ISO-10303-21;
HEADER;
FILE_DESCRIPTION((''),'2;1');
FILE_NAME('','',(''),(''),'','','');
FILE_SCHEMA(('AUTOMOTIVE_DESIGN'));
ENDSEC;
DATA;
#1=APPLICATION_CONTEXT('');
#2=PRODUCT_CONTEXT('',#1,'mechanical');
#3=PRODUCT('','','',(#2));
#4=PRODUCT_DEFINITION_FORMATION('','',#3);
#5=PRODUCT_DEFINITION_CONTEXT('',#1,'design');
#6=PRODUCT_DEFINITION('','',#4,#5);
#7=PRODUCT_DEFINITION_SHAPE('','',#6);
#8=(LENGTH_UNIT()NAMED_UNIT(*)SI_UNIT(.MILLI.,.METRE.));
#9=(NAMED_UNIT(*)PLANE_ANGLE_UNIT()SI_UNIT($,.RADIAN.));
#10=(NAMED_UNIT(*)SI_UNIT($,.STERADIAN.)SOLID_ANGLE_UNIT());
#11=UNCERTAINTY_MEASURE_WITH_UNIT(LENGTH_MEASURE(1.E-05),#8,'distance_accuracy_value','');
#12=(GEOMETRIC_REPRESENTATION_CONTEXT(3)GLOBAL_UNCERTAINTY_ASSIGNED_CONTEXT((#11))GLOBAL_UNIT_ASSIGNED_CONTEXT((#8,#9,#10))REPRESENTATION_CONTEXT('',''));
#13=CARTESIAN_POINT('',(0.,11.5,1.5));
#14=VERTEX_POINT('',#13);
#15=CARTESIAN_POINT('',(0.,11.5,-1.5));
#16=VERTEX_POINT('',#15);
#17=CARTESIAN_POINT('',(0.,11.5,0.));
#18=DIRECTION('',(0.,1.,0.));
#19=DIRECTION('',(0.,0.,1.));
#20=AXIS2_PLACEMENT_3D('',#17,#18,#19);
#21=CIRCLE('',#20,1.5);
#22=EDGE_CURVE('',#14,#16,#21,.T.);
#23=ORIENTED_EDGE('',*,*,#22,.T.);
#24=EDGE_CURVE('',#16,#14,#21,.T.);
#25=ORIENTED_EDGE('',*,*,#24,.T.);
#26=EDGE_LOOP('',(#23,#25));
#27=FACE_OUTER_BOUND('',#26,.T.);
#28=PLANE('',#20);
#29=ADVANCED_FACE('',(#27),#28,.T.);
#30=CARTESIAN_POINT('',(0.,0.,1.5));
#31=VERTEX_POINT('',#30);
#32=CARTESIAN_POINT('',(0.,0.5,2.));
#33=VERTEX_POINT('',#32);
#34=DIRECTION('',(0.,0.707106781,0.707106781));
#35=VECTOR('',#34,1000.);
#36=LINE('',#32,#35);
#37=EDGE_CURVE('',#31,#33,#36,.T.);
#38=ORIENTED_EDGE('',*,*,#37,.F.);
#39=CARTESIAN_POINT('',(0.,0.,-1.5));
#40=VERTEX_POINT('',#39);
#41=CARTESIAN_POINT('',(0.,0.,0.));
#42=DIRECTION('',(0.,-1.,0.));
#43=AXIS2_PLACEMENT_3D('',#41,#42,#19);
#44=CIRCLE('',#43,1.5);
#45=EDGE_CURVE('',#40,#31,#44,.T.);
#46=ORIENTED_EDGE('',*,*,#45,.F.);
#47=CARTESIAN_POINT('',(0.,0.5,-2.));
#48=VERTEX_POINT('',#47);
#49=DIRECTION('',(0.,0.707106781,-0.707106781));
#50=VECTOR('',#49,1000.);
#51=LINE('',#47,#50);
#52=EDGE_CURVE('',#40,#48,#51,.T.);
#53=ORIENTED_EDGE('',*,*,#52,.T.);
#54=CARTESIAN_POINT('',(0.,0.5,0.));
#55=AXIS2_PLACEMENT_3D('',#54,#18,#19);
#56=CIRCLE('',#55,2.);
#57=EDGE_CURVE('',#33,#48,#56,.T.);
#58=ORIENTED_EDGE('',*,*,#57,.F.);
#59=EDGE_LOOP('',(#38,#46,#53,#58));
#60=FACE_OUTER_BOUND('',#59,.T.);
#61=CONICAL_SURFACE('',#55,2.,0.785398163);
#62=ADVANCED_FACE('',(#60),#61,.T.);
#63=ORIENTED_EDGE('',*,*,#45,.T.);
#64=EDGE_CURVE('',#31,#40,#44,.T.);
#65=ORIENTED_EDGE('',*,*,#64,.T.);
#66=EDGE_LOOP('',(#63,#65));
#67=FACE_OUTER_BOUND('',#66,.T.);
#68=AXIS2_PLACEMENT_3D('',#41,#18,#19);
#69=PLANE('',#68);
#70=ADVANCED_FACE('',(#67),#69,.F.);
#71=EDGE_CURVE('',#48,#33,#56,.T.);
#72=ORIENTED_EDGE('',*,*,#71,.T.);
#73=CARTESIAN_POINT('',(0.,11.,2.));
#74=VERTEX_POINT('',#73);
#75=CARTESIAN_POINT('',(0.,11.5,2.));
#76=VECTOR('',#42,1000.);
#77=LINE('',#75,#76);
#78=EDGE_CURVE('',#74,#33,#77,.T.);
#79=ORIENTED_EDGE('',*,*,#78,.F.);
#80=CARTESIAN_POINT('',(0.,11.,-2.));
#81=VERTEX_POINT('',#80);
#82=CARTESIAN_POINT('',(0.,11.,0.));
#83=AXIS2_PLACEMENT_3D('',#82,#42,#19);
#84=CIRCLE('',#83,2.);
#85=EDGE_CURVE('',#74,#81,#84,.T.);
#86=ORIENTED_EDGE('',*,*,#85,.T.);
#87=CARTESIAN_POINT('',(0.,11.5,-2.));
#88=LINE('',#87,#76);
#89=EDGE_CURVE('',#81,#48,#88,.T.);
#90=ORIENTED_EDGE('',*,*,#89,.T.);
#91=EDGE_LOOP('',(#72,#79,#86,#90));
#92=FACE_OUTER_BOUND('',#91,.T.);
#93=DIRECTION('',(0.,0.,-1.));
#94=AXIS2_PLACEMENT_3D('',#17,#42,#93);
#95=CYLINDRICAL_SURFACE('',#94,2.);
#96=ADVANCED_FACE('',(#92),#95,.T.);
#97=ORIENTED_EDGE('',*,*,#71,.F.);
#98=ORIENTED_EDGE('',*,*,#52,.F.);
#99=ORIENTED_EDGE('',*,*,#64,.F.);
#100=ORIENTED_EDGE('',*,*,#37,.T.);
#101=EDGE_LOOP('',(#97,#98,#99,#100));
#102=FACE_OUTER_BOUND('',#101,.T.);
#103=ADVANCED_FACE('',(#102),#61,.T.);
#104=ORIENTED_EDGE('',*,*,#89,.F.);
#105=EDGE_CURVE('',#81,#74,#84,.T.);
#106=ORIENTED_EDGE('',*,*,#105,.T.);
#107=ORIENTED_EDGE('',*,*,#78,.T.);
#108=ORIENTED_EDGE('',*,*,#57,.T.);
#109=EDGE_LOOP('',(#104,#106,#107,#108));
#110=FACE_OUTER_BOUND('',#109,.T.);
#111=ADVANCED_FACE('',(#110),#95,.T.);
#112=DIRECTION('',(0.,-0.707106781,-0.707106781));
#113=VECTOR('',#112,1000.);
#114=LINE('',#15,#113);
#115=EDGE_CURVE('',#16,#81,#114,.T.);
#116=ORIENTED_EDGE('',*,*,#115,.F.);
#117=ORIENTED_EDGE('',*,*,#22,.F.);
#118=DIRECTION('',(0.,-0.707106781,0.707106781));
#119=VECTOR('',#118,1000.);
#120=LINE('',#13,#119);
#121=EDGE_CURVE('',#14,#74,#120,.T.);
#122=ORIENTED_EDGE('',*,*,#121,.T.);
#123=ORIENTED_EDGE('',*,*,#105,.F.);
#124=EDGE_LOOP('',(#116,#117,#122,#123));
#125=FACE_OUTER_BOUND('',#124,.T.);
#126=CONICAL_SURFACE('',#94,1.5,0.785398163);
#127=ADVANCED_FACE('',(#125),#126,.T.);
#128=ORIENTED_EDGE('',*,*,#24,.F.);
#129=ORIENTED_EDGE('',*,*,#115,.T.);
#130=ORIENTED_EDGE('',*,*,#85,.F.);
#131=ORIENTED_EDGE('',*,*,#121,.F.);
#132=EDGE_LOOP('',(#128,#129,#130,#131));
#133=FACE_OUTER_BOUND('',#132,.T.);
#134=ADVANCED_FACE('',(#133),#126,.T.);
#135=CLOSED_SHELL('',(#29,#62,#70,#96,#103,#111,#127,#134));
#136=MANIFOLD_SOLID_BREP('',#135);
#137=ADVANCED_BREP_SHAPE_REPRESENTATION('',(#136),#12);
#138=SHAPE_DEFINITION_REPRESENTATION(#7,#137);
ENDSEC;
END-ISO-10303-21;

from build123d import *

# Parameters (mm, degrees)
PIN_PROFILE_4_R           = 2
PIN_BODY_4X18_DEPTH       = 11.5
END_CHAMFER_A_0_5X45_SIZE = 0.5
END_CHAMFER_B_0_5X45_SIZE = 0.5


with BuildPart() as part:
    # Pin Profile Ø4 → Pin Body Ø4x18 (new body)
    with BuildSketch(Plane(origin=(0, 0, 0), x_dir=(1, 0, 0), z_dir=(0, 1, 0))):
        with Locations(Location((0, 0, 0), (0, 0, 270))):
            Circle(PIN_PROFILE_4_R)
    extrude(amount=PIN_BODY_4X18_DEPTH)

    # End Chamfer A 0.5x45°
    end_chamfer_a_0_5x45_edges = [part.edges().sort_by_distance(p)[0] for p in [
        (0, 11.5, -2),
    ]]
    chamfer(end_chamfer_a_0_5x45_edges, length=END_CHAMFER_A_0_5X45_SIZE)

    # End Chamfer B 0.5x45°
    end_chamfer_b_0_5x45_edges = [part.edges().sort_by_distance(p)[0] for p in [
        (0, 0, -2),
    ]]
    chamfer(end_chamfer_b_0_5x45_edges, length=END_CHAMFER_B_0_5X45_SIZE)


solid = part.part
